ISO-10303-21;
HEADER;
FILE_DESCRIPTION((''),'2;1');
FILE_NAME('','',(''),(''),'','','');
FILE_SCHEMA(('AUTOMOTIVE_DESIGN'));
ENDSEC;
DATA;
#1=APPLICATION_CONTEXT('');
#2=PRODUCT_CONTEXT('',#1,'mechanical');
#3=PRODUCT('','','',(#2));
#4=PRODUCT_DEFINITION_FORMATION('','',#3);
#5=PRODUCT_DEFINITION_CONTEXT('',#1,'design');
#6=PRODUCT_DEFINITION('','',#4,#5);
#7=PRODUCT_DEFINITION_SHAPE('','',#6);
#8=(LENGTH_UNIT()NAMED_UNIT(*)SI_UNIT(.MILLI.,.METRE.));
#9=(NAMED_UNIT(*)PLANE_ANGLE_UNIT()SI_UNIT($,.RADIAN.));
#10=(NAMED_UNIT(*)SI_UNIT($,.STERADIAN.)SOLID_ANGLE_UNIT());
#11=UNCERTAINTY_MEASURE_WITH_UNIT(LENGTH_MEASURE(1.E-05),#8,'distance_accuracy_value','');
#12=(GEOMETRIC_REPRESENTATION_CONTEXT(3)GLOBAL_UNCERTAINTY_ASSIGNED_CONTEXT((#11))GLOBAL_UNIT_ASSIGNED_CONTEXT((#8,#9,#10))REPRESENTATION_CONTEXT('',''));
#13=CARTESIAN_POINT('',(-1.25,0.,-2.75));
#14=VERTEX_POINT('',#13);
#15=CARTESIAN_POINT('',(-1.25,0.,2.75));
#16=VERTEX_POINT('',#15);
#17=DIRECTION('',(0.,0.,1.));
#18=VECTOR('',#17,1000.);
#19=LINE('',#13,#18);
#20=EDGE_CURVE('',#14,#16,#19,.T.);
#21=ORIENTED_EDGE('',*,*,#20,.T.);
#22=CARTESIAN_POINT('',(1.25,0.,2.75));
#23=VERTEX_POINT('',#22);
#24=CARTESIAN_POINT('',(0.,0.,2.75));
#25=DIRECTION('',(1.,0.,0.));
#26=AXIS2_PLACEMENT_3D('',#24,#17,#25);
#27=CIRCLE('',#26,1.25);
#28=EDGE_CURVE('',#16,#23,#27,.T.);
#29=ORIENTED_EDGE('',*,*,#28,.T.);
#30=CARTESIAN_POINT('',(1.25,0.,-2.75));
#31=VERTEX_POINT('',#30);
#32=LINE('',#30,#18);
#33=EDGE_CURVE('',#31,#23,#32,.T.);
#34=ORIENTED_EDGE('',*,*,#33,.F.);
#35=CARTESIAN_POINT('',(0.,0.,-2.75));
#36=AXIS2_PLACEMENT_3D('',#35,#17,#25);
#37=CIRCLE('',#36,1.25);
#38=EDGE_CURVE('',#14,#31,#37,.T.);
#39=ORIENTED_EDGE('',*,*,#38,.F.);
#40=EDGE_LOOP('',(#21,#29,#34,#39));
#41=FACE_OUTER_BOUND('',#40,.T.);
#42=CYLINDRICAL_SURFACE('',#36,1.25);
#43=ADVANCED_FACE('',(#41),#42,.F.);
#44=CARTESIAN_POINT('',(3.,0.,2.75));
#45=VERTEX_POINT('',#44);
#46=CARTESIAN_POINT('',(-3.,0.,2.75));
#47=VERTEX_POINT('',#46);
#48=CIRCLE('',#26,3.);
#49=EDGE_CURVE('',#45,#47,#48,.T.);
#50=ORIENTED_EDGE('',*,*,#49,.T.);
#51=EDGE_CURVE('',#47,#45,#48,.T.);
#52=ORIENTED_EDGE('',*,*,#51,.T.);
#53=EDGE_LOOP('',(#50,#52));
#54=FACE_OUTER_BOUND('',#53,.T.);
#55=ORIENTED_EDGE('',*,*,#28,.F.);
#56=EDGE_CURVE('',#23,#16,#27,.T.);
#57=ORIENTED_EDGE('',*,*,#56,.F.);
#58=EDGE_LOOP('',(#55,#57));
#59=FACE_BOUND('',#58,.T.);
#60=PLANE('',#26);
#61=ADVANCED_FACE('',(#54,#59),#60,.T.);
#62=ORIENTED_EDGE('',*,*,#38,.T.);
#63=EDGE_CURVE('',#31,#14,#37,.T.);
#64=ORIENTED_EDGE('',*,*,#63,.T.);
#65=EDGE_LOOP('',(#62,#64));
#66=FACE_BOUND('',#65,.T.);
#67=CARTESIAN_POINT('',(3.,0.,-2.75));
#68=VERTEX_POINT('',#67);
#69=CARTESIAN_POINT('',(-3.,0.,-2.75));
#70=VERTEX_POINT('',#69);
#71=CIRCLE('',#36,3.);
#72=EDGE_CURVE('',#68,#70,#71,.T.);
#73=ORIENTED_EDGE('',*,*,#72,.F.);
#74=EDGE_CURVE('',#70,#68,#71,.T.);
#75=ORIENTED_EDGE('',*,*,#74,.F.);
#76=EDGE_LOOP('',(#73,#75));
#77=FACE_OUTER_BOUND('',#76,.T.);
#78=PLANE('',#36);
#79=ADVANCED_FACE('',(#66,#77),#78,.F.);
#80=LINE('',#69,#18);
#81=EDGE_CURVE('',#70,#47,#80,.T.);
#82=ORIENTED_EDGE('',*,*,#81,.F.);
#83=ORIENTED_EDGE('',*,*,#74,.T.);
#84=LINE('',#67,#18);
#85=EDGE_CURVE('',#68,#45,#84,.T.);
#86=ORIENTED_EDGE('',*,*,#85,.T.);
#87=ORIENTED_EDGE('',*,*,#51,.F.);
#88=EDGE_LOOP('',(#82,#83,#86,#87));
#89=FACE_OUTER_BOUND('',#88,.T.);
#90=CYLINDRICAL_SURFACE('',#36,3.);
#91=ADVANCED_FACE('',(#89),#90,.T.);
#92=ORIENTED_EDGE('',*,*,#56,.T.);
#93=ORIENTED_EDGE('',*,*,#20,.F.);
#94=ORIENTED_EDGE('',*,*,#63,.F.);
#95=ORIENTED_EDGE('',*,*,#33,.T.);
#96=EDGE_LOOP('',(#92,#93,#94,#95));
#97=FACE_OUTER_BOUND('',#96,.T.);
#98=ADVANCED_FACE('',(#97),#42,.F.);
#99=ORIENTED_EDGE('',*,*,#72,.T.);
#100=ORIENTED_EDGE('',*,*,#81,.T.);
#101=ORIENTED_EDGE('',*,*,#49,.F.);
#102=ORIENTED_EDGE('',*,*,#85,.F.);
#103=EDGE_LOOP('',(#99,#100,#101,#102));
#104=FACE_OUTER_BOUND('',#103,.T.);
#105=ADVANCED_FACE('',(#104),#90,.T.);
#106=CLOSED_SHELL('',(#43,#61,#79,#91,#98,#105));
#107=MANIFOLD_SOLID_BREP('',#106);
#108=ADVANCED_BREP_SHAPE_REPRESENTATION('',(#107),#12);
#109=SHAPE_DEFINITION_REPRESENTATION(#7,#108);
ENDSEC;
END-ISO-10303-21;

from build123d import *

# Parameters (mm, degrees)
SKETCH_1_R      = 3
SKETCH_1_R_2    = 1.25
EXTRUDE_1_DEPTH = 2.75


with BuildPart() as part:
    # 草图1 → 凸台-拉伸1 (new, symmetric)
    with BuildSketch(Plane.XY):
        Circle(SKETCH_1_R)
        Circle(SKETCH_1_R_2, mode=Mode.SUBTRACT)
    extrude(amount=EXTRUDE_1_DEPTH, both=True)


solid = part.part
